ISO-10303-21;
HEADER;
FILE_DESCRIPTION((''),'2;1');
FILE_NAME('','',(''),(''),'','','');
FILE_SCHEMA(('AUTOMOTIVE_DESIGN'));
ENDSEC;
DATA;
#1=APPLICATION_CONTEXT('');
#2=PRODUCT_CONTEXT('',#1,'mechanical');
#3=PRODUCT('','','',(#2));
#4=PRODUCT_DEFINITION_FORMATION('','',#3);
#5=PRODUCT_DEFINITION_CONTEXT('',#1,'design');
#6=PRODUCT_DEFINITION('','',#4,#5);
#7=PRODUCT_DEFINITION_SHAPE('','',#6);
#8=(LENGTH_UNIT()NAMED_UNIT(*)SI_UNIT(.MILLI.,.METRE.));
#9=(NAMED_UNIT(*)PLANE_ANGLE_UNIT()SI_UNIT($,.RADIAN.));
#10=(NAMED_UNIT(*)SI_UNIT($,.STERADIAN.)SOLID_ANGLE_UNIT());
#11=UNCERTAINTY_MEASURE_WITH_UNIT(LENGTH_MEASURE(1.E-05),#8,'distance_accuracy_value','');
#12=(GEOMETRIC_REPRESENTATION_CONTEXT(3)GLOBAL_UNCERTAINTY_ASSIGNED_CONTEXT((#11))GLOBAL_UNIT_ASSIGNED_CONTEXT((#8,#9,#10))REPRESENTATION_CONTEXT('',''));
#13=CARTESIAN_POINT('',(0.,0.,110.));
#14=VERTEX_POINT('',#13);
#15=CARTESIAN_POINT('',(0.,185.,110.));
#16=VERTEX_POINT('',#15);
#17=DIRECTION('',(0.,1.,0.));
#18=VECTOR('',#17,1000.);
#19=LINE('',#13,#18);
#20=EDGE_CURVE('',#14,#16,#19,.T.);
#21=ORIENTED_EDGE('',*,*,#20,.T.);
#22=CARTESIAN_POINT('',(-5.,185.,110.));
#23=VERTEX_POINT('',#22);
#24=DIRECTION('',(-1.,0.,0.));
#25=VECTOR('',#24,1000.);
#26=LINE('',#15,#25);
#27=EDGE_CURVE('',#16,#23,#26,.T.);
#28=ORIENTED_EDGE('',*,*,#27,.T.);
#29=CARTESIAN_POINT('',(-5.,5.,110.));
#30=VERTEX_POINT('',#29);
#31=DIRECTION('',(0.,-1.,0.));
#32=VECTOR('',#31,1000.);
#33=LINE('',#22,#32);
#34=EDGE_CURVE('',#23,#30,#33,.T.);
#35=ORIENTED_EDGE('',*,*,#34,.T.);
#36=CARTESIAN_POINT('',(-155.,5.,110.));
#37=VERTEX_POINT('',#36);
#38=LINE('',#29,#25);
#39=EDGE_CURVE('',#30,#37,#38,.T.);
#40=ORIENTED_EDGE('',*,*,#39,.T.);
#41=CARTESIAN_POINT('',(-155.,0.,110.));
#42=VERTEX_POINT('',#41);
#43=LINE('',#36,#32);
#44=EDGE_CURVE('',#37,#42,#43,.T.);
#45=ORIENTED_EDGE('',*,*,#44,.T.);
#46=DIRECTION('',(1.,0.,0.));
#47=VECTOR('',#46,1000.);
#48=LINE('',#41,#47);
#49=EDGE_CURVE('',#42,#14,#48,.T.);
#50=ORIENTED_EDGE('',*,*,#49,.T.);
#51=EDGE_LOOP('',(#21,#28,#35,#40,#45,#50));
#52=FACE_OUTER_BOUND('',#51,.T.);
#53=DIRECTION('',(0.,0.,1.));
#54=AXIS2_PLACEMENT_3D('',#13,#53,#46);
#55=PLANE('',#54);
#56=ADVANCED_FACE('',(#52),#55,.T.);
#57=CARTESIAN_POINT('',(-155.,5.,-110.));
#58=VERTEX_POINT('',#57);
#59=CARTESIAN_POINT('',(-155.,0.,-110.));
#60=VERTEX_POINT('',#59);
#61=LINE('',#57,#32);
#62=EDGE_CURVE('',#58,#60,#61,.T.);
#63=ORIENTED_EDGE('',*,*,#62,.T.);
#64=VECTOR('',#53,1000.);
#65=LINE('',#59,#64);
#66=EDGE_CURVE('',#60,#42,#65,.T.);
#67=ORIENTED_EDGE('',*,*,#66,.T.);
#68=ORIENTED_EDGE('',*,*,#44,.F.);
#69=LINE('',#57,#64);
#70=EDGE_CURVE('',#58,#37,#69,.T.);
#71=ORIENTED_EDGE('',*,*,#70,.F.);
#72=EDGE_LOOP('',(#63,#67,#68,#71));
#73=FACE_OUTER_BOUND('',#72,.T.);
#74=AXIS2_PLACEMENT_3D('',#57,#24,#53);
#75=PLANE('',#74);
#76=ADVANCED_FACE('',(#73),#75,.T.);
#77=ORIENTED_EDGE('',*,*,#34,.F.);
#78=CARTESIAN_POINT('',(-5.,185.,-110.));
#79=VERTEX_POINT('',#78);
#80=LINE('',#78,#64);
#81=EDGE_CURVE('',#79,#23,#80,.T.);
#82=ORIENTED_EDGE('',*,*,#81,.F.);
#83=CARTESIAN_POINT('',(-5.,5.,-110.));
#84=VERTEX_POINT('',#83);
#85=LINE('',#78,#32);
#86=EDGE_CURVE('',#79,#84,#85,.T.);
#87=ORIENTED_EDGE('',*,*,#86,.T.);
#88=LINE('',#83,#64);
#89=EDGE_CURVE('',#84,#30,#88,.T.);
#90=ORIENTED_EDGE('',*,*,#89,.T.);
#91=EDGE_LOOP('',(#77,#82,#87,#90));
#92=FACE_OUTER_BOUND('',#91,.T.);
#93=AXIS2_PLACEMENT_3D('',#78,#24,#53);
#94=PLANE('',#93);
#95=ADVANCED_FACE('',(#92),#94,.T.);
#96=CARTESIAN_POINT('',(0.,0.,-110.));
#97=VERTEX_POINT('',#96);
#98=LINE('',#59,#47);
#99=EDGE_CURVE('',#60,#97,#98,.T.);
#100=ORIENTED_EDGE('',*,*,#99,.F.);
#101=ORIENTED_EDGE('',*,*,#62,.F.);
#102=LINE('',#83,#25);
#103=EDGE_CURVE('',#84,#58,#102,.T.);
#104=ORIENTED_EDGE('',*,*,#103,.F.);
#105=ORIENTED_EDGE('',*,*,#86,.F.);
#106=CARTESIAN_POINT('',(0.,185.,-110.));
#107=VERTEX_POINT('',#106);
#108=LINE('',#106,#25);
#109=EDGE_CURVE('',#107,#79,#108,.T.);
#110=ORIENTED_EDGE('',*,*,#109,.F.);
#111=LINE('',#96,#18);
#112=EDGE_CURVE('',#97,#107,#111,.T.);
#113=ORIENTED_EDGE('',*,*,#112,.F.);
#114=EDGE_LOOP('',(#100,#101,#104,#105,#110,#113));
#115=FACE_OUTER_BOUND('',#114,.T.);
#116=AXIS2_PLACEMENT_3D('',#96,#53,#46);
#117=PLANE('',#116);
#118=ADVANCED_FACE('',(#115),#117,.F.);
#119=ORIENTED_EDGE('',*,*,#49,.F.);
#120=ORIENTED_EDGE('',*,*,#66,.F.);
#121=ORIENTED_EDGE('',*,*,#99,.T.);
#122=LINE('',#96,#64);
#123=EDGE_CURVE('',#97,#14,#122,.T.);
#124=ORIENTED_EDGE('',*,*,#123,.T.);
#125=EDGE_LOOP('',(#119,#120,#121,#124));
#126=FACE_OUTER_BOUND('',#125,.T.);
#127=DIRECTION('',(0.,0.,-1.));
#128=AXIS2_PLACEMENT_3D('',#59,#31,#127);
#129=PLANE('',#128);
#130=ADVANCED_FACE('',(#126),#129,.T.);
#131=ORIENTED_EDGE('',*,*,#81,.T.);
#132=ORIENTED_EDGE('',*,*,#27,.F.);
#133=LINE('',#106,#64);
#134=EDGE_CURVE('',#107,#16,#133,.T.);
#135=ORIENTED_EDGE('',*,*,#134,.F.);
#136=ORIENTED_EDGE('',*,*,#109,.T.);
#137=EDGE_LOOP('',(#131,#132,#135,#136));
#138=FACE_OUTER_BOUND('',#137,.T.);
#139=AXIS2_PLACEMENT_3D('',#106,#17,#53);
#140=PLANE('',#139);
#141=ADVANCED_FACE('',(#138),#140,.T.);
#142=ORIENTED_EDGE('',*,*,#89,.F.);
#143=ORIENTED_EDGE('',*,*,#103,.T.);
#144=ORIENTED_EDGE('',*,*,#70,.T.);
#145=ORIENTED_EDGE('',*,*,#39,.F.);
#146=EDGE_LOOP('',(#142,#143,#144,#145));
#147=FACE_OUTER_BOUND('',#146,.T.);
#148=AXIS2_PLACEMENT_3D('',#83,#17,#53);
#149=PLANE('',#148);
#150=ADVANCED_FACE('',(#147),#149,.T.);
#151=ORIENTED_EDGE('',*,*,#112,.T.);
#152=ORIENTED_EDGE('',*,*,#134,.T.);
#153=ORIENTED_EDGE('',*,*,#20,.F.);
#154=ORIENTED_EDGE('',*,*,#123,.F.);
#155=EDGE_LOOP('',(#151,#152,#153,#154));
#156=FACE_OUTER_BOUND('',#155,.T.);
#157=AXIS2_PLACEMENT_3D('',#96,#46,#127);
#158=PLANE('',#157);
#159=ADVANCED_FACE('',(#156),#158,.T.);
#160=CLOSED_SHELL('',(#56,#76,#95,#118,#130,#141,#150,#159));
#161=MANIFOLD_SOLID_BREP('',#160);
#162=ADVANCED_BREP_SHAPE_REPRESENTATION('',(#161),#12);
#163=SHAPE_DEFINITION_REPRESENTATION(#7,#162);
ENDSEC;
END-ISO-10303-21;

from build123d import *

# Parameters (mm, degrees)
EXTRUDE_1_DEPTH = 110


with BuildPart() as part:
    # 草图1 → 凸台-拉伸1 (new, symmetric)
    with BuildSketch(Plane.XY):
        Polygon((-155, 0), (0, 0), (0, 185), (-5, 185), (-5, 5), (-155, 5), align=None)
    extrude(amount=EXTRUDE_1_DEPTH, both=True)


solid = part.part
